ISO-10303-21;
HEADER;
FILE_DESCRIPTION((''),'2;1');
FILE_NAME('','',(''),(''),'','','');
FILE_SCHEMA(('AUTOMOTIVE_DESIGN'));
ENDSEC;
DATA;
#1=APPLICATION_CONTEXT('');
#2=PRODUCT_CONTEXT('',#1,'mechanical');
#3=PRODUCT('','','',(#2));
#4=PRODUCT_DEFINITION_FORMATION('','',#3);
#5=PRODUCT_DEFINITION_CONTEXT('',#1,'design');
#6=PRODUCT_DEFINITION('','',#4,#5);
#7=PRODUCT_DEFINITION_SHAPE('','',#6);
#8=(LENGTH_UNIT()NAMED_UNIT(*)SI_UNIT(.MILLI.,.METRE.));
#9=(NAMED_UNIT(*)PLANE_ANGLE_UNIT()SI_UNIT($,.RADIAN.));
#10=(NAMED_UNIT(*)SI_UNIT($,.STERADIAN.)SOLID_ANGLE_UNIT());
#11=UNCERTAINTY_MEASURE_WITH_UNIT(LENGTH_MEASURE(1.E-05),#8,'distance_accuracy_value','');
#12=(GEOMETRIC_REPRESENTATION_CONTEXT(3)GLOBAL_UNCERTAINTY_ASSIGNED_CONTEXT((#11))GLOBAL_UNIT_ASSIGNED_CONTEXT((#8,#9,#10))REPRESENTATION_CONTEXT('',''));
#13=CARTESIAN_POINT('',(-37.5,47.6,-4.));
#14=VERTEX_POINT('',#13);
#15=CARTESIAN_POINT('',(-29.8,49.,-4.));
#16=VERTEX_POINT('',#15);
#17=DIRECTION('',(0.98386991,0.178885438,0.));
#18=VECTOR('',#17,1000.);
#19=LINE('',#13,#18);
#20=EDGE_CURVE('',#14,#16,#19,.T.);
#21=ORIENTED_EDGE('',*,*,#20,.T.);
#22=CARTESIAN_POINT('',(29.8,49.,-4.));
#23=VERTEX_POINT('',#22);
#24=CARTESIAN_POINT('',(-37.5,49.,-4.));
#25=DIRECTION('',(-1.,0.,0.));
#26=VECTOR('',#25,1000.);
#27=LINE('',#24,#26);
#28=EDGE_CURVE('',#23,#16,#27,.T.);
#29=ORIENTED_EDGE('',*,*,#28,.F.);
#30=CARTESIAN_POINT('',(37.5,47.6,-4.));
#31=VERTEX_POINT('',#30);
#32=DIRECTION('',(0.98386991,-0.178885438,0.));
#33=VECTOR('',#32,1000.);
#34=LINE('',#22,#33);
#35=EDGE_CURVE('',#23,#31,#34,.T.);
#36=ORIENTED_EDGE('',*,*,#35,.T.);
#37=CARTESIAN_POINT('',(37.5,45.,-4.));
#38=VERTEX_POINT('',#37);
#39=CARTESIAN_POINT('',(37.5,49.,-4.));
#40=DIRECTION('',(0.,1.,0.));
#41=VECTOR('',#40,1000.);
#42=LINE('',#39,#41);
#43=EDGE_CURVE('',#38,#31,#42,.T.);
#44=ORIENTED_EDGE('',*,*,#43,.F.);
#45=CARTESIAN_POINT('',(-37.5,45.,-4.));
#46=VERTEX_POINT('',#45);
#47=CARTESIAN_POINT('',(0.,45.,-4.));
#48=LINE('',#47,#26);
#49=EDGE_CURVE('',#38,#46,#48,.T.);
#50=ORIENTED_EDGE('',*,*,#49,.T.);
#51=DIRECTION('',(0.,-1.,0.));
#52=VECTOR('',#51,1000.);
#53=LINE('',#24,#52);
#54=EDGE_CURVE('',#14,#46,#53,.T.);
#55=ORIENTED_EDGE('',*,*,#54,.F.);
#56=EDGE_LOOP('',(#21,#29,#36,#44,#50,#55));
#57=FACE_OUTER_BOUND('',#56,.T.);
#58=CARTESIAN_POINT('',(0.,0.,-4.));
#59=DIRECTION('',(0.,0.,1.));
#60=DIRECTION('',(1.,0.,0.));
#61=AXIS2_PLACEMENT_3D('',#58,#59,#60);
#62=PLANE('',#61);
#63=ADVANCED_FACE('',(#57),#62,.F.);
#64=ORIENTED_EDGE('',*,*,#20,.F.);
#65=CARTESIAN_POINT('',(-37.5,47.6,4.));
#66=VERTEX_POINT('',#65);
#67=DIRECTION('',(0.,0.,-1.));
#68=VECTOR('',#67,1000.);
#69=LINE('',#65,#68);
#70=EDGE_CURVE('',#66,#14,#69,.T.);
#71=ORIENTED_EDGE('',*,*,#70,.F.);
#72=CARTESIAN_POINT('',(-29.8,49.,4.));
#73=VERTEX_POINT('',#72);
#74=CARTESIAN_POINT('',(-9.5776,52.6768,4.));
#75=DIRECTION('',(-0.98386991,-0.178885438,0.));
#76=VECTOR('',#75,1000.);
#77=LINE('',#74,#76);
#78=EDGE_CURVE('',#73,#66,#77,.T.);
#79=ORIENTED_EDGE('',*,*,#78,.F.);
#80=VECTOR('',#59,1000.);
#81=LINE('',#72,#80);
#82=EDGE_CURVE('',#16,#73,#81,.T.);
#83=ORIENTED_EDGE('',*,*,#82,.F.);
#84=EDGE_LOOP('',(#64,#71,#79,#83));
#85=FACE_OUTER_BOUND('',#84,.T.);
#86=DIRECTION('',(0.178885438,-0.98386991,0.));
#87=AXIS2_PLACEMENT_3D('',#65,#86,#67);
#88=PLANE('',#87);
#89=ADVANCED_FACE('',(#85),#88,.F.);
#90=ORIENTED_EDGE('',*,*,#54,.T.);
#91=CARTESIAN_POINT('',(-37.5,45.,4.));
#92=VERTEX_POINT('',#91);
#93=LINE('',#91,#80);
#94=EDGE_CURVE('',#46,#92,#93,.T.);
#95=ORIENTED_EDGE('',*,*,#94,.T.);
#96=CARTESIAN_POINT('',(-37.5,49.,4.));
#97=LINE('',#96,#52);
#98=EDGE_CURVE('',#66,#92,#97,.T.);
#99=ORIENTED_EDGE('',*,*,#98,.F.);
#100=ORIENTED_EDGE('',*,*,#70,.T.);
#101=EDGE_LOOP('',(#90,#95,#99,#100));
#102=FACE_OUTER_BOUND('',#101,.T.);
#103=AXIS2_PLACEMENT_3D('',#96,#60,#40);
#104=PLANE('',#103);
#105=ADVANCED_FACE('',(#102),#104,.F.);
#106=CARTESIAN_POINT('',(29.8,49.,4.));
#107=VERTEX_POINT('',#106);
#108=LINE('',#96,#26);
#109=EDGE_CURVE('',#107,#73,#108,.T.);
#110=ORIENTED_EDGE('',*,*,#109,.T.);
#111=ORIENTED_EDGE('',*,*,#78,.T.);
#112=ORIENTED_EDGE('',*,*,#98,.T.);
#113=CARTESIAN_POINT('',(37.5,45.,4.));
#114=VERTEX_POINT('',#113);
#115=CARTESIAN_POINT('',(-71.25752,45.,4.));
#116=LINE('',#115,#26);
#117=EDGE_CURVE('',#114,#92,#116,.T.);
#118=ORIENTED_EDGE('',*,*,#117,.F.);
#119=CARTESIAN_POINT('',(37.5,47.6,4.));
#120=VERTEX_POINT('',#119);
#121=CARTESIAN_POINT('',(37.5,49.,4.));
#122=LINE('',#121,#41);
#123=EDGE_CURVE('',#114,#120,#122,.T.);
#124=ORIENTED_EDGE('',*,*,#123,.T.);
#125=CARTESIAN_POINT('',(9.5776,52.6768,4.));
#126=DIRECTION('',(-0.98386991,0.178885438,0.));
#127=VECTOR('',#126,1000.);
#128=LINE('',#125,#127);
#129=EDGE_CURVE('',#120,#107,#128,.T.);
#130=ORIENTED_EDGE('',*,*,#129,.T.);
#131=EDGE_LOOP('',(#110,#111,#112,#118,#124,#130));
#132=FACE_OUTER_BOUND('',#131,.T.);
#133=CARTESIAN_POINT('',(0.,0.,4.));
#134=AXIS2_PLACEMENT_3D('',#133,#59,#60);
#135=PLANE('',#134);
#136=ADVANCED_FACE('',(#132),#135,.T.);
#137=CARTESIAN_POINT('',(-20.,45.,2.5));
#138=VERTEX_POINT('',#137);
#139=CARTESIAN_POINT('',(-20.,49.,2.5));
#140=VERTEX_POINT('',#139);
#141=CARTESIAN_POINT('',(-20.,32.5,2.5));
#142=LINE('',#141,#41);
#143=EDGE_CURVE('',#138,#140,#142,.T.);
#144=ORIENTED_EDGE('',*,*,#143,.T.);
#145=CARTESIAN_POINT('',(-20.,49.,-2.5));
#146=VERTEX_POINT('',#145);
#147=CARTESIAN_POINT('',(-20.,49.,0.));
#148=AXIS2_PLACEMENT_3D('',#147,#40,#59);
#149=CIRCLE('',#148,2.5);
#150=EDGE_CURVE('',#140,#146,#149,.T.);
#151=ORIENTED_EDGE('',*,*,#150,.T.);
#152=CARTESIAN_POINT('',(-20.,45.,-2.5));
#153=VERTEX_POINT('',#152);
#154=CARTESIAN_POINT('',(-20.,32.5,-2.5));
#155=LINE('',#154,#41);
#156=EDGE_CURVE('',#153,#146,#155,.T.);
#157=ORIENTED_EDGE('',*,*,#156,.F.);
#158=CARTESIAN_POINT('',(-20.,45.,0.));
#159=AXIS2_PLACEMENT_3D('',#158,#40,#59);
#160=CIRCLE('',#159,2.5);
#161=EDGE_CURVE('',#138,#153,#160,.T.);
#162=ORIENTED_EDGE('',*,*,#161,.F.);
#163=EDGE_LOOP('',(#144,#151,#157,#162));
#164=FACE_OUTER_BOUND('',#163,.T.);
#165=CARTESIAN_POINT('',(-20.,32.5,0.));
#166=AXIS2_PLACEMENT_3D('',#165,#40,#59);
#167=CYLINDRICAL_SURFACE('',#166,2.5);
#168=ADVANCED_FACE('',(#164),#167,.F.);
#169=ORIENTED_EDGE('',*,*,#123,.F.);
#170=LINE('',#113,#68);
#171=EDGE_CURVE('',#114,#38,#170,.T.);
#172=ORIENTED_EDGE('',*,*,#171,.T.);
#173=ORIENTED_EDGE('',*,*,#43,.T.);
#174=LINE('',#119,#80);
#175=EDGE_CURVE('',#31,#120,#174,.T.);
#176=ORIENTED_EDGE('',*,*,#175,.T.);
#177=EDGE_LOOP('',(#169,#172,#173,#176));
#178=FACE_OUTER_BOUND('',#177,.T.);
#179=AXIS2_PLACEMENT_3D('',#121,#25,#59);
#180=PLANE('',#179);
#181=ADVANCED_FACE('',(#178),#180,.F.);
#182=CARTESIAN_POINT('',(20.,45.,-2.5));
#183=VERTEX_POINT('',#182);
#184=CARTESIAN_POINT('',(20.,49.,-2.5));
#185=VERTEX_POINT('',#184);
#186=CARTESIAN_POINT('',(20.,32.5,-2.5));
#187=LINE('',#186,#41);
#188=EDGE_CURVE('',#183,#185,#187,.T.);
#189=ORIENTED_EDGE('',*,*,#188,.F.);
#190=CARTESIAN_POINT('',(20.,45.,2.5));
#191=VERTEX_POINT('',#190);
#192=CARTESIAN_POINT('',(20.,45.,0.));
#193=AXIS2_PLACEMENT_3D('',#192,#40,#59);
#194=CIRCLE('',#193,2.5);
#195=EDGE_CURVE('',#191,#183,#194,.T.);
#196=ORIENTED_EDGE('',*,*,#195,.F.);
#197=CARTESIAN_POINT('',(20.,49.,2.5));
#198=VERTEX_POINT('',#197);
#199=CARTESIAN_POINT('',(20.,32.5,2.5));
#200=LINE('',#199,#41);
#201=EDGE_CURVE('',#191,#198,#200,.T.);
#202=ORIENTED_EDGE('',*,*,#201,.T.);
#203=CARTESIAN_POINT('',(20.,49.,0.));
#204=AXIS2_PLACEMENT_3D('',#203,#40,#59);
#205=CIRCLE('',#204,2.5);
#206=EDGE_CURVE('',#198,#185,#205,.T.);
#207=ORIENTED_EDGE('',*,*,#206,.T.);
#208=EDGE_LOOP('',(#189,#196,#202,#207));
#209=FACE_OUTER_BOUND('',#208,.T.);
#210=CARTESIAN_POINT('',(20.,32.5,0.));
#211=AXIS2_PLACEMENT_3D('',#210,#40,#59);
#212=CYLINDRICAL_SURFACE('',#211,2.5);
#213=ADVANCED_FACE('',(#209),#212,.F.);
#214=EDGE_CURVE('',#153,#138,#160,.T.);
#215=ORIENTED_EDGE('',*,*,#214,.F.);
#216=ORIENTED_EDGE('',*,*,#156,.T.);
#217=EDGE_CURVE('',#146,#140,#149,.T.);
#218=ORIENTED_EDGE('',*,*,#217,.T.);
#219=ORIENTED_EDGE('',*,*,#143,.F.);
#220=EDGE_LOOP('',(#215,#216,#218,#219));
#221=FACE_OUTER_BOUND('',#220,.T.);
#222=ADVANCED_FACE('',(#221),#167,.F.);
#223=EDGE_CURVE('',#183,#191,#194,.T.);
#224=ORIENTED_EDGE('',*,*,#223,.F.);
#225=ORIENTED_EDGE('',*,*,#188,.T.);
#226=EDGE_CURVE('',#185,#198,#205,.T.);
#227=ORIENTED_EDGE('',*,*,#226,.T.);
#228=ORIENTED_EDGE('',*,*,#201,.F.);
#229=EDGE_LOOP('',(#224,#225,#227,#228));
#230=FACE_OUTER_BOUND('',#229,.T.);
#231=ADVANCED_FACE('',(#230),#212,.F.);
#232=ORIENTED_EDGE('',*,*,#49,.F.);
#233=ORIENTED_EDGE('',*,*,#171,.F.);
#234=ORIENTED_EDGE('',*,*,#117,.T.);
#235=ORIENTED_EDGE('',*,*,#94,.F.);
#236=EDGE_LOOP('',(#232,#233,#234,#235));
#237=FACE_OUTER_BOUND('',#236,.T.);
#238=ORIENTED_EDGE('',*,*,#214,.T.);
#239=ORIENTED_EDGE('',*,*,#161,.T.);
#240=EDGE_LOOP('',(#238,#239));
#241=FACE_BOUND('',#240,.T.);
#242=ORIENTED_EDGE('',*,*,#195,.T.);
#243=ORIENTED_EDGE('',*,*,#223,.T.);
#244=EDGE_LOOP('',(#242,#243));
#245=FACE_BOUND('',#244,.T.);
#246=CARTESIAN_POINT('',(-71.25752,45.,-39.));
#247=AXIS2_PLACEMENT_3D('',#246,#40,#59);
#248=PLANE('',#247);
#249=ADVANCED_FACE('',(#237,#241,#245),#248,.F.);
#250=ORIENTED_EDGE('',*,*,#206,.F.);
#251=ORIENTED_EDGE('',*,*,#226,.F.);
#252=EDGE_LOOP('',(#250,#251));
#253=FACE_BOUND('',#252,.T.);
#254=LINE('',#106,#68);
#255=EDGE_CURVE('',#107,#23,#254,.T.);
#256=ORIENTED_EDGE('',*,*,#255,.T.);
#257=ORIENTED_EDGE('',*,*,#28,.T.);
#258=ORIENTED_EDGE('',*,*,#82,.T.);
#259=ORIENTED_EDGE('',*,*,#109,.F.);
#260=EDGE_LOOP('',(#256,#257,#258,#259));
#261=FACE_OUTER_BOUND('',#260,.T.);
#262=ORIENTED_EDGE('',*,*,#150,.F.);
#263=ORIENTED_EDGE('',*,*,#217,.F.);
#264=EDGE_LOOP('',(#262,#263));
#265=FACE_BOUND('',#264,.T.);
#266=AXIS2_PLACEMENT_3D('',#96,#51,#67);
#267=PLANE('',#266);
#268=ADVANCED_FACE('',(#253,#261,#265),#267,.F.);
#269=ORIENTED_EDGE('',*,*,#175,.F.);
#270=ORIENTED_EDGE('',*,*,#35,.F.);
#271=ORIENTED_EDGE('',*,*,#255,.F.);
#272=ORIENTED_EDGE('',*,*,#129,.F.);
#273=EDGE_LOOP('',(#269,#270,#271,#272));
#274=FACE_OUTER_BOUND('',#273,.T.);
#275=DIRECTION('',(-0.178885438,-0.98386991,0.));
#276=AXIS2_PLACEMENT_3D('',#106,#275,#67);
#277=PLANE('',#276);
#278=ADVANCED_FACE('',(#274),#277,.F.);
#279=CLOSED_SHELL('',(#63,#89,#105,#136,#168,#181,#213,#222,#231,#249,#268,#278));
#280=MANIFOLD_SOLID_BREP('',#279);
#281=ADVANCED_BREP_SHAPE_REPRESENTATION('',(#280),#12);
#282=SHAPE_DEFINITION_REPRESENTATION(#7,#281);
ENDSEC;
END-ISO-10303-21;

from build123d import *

# Parameters (mm, degrees)
SKETCH_1_W                = 100
SKETCH_1_H                = 136
EXTRUDE_1_DEPTH           = 4
SKETCH_3_W                = 75
SKETCH_3_H                = 15
EXTRUDE_2_DEPTH           = 4
CHAMFER_2_SIZE            = 7.7
CHAMFER_2_SIZE2           = 1.4
CHAMFER_3_SIZE            = 1.4
CHAMFER_3_SIZE2           = 7.7
FILLET_1_R                = 5
CHAMFER_4_SIZE            = 3
HOLE_WIZARD_M4_1_D        = 3.3
HOLE_WIZARD_M4_1_DEPTH    = 11.5
HOLE_WIZARD_M4_1_TIP      = 0.991420021
SKETCH_8_W                = 362.353371429
SKETCH_8_H                = 115.701942857
CUT_EXTRUDE_4_DEPTH       = 114.877126764
CHAMFER_5_SIZE            = 3
HOLE_WIZARD_1_D           = 4.5
HOLE_WIZARD_1_CBORE_D     = 8
HOLE_WIZARD_1_CBORE_DEPTH = 5
CHAMFER_6_SIZE            = 3
SKETCH_14_W               = 127.06003401
SKETCH_14_H               = 84.591980831
CUT_EXTRUDE_5_DEPTH       = 43
SKETCH_15_R               = 2.5
CUT_EXTRUDE_6_DEPTH       = 16.5


with BuildPart() as part:
    # 草图1 → 凸台-拉伸1 (new, symmetric)
    with BuildSketch(Plane.XY):
        with Locations((0, -34)):
            Rectangle(SKETCH_1_W, SKETCH_1_H)
    extrude(amount=EXTRUDE_1_DEPTH, both=True)

    # 草图3 → 凸台-拉伸2 (add, symmetric)
    with BuildSketch(Plane.XY):
        with Locations((0, 41.5)):
            Rectangle(SKETCH_3_W, SKETCH_3_H)
    extrude(amount=EXTRUDE_2_DEPTH, both=True)

    # 倒角2
    chamfer_2_edges = [part.edges().sort_by_distance(p)[0] for p in [
        (-37.5, 49, 0),
    ]]
    chamfer_2_side = [part.faces().sort_by_distance(p)[0] for p in [
        (0, 49, 0),
    ]]
    chamfer(chamfer_2_edges, length=CHAMFER_2_SIZE, length2=CHAMFER_2_SIZE2, reference=chamfer_2_side[0])

    # 倒角3
    chamfer_3_edges = [part.edges().sort_by_distance(p)[0] for p in [
        (37.5, 49, 0),
    ]]
    chamfer_3_side = [part.faces().sort_by_distance(p)[0] for p in [
        (37.5, 41.5, 0),
    ]]
    chamfer(chamfer_3_edges, length=CHAMFER_3_SIZE, length2=CHAMFER_3_SIZE2, reference=chamfer_3_side[0])

    # 圆角1
    fillet_1_edges = [part.edges().sort_by_distance(p)[0] for p in [
        (-37.5, 34, 0),
        (37.5, 34, 0),
    ]]
    fillet(fillet_1_edges, radius=FILLET_1_R)

    # 倒角4
    chamfer_4_edges = [part.edges().sort_by_distance(p)[0] for p in [
        (50, -102, 0),
        (-50, -102, 0),
    ]]
    chamfer(chamfer_4_edges, length=CHAMFER_4_SIZE)

    # M4 螺纹孔1
    with Locations(Plane(origin=(0, 49, 0), x_dir=(1, 0, 0), z_dir=(0, 1, 0))):
        with Locations((-20, 0), (20, 0)):
            Hole(HOLE_WIZARD_M4_1_D / 2, depth=HOLE_WIZARD_M4_1_DEPTH)
            with Locations((0, 0, -(HOLE_WIZARD_M4_1_DEPTH + HOLE_WIZARD_M4_1_TIP / 2))):  # 118° drill point
                Cone(0, HOLE_WIZARD_M4_1_D / 2, HOLE_WIZARD_M4_1_TIP, mode=Mode.SUBTRACT)

    # 草图8 → 切除-拉伸4 (cut, through all)
    with BuildSketch(Plane(origin=(0, 0, -4), x_dir=(-1, 0, 0), z_dir=(0, 0, -1))):
        with Locations((78.704228572, -69.850971429)):
            Rectangle(SKETCH_8_W, SKETCH_8_H)
    extrude(amount=-CUT_EXTRUDE_4_DEPTH, mode=Mode.SUBTRACT)

    # 倒角5
    chamfer_5_edges = [part.edges().sort_by_distance(p)[0] for p in [
        (-50, -12, 0),
        (50, -12, 0),
    ]]
    chamfer(chamfer_5_edges, length=CHAMFER_5_SIZE)

    # 打孔尺寸(%根据)开槽圆柱头螺钉的类型1 (through all)
    with Locations(Plane.XY.offset(4)):
        with Locations((-43.15, -3), (43.15, -3), (-45, 29), (45, 29)):
            CounterBoreHole(HOLE_WIZARD_1_D / 2, HOLE_WIZARD_1_CBORE_D / 2, HOLE_WIZARD_1_CBORE_DEPTH)

    # 倒角6
    chamfer_6_edges = [part.edges().sort_by_distance(p)[0] for p in [
        (-50, 34, 0),
        (50, 34, 0),
    ]]
    chamfer(chamfer_6_edges, length=CHAMFER_6_SIZE)

    # 草图14 → 切除-拉伸5 (cut)
    with BuildSketch(Plane.XY.offset(4)):
        with Locations((-7.727502701, 2.704009584)):
            Rectangle(SKETCH_14_W, SKETCH_14_H)
    extrude(amount=-CUT_EXTRUDE_5_DEPTH, mode=Mode.SUBTRACT)

    # 草图15 → 切除-拉伸6 (cut)
    with BuildSketch(Plane(origin=(0, 49, 0), x_dir=(1, 0, 0), z_dir=(0, 1, 0))):
        with Locations(Location((-20, 0, 0), (0, 0, 270))):
            Circle(SKETCH_15_R)
        with Locations(Location((20, 0, 0), (0, 0, 270))):
            Circle(SKETCH_15_R)
    extrude(amount=-CUT_EXTRUDE_6_DEPTH, mode=Mode.SUBTRACT)


solid = part.part
